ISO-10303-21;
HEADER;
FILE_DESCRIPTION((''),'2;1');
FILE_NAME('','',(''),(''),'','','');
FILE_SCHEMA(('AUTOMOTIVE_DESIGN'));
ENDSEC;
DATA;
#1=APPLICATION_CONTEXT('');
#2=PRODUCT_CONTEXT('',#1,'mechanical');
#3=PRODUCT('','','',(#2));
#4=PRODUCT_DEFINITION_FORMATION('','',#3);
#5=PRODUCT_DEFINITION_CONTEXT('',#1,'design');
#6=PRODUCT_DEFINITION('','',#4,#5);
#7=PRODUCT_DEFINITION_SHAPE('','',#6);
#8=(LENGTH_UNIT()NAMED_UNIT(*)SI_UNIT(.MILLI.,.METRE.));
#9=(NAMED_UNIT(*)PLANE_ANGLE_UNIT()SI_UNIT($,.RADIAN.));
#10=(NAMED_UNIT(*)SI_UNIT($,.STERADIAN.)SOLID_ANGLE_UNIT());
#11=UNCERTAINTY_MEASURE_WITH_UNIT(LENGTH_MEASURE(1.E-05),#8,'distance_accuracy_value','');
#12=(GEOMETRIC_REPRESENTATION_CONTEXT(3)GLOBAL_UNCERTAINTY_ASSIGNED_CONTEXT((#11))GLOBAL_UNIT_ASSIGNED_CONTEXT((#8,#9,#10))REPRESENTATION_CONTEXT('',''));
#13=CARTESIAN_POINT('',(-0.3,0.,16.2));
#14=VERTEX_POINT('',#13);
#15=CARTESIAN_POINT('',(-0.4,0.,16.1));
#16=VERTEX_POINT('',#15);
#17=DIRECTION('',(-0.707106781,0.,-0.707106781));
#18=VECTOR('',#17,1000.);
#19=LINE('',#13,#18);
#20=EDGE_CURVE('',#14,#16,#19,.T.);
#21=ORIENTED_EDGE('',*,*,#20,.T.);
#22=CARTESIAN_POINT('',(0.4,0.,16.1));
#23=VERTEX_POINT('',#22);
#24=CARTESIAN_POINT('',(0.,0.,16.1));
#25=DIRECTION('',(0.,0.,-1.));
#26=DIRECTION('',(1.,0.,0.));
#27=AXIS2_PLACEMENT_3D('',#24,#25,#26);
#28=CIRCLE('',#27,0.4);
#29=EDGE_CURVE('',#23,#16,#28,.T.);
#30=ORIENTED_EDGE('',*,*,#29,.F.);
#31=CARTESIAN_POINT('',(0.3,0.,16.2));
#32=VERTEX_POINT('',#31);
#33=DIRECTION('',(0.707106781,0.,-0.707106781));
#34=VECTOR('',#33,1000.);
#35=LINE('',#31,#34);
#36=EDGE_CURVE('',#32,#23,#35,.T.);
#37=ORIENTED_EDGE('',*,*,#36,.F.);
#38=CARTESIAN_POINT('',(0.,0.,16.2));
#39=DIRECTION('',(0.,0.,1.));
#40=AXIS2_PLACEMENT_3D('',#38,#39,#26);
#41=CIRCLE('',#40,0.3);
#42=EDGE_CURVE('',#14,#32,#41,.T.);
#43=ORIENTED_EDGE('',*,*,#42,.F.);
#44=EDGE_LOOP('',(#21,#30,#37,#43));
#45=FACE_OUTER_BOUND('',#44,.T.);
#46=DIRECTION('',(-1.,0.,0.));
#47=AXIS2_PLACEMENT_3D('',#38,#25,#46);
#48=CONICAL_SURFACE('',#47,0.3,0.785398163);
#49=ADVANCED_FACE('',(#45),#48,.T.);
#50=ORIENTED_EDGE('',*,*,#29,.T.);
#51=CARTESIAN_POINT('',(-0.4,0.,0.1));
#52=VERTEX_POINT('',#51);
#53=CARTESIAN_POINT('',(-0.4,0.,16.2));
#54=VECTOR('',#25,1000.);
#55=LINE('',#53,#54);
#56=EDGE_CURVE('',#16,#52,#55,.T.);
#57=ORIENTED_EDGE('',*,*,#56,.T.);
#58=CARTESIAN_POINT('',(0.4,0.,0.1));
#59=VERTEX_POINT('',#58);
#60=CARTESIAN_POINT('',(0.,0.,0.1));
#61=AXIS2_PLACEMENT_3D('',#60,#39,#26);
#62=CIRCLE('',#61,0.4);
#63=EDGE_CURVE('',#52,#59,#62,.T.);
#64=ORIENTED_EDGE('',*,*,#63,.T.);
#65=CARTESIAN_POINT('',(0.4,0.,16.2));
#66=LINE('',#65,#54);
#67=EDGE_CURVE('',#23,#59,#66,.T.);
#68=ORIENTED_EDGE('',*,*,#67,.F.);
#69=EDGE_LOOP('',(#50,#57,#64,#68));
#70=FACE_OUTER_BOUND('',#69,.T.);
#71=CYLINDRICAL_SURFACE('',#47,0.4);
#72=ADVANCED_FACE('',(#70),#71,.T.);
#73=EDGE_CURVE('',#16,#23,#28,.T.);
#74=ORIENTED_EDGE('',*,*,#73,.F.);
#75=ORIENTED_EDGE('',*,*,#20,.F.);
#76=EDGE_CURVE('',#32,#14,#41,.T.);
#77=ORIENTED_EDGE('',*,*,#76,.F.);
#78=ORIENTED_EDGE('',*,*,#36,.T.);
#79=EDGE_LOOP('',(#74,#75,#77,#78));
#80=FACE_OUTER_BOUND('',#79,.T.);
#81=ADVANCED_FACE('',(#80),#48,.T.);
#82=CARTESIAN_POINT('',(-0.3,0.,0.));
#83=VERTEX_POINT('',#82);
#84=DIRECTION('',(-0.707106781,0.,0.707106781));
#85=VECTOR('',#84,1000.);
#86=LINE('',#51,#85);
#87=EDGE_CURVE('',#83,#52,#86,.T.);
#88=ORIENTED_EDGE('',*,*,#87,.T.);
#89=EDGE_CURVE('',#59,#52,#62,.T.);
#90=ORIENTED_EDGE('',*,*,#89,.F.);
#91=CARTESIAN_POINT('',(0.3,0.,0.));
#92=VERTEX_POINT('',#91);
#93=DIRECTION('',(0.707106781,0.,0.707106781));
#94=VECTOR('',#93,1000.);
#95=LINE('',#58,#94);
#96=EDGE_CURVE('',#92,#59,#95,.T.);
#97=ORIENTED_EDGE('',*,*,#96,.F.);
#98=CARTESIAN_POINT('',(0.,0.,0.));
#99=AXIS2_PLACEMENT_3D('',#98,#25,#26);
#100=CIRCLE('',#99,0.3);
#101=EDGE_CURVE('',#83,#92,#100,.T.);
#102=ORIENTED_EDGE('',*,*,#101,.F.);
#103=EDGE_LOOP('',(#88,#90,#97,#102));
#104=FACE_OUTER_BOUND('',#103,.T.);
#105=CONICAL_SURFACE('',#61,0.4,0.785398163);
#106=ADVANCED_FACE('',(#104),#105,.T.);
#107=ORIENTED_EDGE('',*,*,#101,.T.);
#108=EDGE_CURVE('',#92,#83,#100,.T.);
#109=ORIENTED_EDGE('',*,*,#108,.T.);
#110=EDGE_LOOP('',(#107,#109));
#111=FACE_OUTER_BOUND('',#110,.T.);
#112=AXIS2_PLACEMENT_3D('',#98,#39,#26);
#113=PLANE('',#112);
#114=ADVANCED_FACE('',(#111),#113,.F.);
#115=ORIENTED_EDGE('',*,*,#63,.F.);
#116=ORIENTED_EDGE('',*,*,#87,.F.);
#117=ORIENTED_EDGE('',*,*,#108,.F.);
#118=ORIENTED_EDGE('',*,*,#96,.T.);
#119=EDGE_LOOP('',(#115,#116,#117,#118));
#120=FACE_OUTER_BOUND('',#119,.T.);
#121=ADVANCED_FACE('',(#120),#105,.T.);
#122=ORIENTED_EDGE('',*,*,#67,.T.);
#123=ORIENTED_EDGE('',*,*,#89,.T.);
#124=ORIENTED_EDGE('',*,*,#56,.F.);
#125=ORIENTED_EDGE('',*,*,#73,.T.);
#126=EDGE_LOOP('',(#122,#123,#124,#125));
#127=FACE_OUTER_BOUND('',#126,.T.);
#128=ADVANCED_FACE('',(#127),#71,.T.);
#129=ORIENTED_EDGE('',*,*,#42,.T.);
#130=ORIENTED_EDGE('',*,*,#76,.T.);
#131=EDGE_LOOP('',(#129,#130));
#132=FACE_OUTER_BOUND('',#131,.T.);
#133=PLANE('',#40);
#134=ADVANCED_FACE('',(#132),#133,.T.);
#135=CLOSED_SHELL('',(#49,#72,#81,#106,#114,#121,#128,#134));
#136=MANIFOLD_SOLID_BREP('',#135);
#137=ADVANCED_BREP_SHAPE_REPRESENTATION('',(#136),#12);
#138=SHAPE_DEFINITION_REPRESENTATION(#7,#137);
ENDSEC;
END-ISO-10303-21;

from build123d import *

# Parameters (mm, degrees)
SKETCH1_R           = 0.4
BOSS_EXTRUDE1_DEPTH = 16.2
CHAMFER1_SIZE       = 0.1


with BuildPart() as part:
    # Sketch1 → Boss-Extrude1 (new body)
    with BuildSketch(Plane.XY):
        Circle(SKETCH1_R)
    extrude(amount=BOSS_EXTRUDE1_DEPTH)

    # Chamfer1
    chamfer1_edges = [part.edges().sort_by_distance(p)[0] for p in [
        (-0.4, 0, 0),
        (-0.4, 0, 16.2),
    ]]
    chamfer(chamfer1_edges, length=CHAMFER1_SIZE)


solid = part.part
